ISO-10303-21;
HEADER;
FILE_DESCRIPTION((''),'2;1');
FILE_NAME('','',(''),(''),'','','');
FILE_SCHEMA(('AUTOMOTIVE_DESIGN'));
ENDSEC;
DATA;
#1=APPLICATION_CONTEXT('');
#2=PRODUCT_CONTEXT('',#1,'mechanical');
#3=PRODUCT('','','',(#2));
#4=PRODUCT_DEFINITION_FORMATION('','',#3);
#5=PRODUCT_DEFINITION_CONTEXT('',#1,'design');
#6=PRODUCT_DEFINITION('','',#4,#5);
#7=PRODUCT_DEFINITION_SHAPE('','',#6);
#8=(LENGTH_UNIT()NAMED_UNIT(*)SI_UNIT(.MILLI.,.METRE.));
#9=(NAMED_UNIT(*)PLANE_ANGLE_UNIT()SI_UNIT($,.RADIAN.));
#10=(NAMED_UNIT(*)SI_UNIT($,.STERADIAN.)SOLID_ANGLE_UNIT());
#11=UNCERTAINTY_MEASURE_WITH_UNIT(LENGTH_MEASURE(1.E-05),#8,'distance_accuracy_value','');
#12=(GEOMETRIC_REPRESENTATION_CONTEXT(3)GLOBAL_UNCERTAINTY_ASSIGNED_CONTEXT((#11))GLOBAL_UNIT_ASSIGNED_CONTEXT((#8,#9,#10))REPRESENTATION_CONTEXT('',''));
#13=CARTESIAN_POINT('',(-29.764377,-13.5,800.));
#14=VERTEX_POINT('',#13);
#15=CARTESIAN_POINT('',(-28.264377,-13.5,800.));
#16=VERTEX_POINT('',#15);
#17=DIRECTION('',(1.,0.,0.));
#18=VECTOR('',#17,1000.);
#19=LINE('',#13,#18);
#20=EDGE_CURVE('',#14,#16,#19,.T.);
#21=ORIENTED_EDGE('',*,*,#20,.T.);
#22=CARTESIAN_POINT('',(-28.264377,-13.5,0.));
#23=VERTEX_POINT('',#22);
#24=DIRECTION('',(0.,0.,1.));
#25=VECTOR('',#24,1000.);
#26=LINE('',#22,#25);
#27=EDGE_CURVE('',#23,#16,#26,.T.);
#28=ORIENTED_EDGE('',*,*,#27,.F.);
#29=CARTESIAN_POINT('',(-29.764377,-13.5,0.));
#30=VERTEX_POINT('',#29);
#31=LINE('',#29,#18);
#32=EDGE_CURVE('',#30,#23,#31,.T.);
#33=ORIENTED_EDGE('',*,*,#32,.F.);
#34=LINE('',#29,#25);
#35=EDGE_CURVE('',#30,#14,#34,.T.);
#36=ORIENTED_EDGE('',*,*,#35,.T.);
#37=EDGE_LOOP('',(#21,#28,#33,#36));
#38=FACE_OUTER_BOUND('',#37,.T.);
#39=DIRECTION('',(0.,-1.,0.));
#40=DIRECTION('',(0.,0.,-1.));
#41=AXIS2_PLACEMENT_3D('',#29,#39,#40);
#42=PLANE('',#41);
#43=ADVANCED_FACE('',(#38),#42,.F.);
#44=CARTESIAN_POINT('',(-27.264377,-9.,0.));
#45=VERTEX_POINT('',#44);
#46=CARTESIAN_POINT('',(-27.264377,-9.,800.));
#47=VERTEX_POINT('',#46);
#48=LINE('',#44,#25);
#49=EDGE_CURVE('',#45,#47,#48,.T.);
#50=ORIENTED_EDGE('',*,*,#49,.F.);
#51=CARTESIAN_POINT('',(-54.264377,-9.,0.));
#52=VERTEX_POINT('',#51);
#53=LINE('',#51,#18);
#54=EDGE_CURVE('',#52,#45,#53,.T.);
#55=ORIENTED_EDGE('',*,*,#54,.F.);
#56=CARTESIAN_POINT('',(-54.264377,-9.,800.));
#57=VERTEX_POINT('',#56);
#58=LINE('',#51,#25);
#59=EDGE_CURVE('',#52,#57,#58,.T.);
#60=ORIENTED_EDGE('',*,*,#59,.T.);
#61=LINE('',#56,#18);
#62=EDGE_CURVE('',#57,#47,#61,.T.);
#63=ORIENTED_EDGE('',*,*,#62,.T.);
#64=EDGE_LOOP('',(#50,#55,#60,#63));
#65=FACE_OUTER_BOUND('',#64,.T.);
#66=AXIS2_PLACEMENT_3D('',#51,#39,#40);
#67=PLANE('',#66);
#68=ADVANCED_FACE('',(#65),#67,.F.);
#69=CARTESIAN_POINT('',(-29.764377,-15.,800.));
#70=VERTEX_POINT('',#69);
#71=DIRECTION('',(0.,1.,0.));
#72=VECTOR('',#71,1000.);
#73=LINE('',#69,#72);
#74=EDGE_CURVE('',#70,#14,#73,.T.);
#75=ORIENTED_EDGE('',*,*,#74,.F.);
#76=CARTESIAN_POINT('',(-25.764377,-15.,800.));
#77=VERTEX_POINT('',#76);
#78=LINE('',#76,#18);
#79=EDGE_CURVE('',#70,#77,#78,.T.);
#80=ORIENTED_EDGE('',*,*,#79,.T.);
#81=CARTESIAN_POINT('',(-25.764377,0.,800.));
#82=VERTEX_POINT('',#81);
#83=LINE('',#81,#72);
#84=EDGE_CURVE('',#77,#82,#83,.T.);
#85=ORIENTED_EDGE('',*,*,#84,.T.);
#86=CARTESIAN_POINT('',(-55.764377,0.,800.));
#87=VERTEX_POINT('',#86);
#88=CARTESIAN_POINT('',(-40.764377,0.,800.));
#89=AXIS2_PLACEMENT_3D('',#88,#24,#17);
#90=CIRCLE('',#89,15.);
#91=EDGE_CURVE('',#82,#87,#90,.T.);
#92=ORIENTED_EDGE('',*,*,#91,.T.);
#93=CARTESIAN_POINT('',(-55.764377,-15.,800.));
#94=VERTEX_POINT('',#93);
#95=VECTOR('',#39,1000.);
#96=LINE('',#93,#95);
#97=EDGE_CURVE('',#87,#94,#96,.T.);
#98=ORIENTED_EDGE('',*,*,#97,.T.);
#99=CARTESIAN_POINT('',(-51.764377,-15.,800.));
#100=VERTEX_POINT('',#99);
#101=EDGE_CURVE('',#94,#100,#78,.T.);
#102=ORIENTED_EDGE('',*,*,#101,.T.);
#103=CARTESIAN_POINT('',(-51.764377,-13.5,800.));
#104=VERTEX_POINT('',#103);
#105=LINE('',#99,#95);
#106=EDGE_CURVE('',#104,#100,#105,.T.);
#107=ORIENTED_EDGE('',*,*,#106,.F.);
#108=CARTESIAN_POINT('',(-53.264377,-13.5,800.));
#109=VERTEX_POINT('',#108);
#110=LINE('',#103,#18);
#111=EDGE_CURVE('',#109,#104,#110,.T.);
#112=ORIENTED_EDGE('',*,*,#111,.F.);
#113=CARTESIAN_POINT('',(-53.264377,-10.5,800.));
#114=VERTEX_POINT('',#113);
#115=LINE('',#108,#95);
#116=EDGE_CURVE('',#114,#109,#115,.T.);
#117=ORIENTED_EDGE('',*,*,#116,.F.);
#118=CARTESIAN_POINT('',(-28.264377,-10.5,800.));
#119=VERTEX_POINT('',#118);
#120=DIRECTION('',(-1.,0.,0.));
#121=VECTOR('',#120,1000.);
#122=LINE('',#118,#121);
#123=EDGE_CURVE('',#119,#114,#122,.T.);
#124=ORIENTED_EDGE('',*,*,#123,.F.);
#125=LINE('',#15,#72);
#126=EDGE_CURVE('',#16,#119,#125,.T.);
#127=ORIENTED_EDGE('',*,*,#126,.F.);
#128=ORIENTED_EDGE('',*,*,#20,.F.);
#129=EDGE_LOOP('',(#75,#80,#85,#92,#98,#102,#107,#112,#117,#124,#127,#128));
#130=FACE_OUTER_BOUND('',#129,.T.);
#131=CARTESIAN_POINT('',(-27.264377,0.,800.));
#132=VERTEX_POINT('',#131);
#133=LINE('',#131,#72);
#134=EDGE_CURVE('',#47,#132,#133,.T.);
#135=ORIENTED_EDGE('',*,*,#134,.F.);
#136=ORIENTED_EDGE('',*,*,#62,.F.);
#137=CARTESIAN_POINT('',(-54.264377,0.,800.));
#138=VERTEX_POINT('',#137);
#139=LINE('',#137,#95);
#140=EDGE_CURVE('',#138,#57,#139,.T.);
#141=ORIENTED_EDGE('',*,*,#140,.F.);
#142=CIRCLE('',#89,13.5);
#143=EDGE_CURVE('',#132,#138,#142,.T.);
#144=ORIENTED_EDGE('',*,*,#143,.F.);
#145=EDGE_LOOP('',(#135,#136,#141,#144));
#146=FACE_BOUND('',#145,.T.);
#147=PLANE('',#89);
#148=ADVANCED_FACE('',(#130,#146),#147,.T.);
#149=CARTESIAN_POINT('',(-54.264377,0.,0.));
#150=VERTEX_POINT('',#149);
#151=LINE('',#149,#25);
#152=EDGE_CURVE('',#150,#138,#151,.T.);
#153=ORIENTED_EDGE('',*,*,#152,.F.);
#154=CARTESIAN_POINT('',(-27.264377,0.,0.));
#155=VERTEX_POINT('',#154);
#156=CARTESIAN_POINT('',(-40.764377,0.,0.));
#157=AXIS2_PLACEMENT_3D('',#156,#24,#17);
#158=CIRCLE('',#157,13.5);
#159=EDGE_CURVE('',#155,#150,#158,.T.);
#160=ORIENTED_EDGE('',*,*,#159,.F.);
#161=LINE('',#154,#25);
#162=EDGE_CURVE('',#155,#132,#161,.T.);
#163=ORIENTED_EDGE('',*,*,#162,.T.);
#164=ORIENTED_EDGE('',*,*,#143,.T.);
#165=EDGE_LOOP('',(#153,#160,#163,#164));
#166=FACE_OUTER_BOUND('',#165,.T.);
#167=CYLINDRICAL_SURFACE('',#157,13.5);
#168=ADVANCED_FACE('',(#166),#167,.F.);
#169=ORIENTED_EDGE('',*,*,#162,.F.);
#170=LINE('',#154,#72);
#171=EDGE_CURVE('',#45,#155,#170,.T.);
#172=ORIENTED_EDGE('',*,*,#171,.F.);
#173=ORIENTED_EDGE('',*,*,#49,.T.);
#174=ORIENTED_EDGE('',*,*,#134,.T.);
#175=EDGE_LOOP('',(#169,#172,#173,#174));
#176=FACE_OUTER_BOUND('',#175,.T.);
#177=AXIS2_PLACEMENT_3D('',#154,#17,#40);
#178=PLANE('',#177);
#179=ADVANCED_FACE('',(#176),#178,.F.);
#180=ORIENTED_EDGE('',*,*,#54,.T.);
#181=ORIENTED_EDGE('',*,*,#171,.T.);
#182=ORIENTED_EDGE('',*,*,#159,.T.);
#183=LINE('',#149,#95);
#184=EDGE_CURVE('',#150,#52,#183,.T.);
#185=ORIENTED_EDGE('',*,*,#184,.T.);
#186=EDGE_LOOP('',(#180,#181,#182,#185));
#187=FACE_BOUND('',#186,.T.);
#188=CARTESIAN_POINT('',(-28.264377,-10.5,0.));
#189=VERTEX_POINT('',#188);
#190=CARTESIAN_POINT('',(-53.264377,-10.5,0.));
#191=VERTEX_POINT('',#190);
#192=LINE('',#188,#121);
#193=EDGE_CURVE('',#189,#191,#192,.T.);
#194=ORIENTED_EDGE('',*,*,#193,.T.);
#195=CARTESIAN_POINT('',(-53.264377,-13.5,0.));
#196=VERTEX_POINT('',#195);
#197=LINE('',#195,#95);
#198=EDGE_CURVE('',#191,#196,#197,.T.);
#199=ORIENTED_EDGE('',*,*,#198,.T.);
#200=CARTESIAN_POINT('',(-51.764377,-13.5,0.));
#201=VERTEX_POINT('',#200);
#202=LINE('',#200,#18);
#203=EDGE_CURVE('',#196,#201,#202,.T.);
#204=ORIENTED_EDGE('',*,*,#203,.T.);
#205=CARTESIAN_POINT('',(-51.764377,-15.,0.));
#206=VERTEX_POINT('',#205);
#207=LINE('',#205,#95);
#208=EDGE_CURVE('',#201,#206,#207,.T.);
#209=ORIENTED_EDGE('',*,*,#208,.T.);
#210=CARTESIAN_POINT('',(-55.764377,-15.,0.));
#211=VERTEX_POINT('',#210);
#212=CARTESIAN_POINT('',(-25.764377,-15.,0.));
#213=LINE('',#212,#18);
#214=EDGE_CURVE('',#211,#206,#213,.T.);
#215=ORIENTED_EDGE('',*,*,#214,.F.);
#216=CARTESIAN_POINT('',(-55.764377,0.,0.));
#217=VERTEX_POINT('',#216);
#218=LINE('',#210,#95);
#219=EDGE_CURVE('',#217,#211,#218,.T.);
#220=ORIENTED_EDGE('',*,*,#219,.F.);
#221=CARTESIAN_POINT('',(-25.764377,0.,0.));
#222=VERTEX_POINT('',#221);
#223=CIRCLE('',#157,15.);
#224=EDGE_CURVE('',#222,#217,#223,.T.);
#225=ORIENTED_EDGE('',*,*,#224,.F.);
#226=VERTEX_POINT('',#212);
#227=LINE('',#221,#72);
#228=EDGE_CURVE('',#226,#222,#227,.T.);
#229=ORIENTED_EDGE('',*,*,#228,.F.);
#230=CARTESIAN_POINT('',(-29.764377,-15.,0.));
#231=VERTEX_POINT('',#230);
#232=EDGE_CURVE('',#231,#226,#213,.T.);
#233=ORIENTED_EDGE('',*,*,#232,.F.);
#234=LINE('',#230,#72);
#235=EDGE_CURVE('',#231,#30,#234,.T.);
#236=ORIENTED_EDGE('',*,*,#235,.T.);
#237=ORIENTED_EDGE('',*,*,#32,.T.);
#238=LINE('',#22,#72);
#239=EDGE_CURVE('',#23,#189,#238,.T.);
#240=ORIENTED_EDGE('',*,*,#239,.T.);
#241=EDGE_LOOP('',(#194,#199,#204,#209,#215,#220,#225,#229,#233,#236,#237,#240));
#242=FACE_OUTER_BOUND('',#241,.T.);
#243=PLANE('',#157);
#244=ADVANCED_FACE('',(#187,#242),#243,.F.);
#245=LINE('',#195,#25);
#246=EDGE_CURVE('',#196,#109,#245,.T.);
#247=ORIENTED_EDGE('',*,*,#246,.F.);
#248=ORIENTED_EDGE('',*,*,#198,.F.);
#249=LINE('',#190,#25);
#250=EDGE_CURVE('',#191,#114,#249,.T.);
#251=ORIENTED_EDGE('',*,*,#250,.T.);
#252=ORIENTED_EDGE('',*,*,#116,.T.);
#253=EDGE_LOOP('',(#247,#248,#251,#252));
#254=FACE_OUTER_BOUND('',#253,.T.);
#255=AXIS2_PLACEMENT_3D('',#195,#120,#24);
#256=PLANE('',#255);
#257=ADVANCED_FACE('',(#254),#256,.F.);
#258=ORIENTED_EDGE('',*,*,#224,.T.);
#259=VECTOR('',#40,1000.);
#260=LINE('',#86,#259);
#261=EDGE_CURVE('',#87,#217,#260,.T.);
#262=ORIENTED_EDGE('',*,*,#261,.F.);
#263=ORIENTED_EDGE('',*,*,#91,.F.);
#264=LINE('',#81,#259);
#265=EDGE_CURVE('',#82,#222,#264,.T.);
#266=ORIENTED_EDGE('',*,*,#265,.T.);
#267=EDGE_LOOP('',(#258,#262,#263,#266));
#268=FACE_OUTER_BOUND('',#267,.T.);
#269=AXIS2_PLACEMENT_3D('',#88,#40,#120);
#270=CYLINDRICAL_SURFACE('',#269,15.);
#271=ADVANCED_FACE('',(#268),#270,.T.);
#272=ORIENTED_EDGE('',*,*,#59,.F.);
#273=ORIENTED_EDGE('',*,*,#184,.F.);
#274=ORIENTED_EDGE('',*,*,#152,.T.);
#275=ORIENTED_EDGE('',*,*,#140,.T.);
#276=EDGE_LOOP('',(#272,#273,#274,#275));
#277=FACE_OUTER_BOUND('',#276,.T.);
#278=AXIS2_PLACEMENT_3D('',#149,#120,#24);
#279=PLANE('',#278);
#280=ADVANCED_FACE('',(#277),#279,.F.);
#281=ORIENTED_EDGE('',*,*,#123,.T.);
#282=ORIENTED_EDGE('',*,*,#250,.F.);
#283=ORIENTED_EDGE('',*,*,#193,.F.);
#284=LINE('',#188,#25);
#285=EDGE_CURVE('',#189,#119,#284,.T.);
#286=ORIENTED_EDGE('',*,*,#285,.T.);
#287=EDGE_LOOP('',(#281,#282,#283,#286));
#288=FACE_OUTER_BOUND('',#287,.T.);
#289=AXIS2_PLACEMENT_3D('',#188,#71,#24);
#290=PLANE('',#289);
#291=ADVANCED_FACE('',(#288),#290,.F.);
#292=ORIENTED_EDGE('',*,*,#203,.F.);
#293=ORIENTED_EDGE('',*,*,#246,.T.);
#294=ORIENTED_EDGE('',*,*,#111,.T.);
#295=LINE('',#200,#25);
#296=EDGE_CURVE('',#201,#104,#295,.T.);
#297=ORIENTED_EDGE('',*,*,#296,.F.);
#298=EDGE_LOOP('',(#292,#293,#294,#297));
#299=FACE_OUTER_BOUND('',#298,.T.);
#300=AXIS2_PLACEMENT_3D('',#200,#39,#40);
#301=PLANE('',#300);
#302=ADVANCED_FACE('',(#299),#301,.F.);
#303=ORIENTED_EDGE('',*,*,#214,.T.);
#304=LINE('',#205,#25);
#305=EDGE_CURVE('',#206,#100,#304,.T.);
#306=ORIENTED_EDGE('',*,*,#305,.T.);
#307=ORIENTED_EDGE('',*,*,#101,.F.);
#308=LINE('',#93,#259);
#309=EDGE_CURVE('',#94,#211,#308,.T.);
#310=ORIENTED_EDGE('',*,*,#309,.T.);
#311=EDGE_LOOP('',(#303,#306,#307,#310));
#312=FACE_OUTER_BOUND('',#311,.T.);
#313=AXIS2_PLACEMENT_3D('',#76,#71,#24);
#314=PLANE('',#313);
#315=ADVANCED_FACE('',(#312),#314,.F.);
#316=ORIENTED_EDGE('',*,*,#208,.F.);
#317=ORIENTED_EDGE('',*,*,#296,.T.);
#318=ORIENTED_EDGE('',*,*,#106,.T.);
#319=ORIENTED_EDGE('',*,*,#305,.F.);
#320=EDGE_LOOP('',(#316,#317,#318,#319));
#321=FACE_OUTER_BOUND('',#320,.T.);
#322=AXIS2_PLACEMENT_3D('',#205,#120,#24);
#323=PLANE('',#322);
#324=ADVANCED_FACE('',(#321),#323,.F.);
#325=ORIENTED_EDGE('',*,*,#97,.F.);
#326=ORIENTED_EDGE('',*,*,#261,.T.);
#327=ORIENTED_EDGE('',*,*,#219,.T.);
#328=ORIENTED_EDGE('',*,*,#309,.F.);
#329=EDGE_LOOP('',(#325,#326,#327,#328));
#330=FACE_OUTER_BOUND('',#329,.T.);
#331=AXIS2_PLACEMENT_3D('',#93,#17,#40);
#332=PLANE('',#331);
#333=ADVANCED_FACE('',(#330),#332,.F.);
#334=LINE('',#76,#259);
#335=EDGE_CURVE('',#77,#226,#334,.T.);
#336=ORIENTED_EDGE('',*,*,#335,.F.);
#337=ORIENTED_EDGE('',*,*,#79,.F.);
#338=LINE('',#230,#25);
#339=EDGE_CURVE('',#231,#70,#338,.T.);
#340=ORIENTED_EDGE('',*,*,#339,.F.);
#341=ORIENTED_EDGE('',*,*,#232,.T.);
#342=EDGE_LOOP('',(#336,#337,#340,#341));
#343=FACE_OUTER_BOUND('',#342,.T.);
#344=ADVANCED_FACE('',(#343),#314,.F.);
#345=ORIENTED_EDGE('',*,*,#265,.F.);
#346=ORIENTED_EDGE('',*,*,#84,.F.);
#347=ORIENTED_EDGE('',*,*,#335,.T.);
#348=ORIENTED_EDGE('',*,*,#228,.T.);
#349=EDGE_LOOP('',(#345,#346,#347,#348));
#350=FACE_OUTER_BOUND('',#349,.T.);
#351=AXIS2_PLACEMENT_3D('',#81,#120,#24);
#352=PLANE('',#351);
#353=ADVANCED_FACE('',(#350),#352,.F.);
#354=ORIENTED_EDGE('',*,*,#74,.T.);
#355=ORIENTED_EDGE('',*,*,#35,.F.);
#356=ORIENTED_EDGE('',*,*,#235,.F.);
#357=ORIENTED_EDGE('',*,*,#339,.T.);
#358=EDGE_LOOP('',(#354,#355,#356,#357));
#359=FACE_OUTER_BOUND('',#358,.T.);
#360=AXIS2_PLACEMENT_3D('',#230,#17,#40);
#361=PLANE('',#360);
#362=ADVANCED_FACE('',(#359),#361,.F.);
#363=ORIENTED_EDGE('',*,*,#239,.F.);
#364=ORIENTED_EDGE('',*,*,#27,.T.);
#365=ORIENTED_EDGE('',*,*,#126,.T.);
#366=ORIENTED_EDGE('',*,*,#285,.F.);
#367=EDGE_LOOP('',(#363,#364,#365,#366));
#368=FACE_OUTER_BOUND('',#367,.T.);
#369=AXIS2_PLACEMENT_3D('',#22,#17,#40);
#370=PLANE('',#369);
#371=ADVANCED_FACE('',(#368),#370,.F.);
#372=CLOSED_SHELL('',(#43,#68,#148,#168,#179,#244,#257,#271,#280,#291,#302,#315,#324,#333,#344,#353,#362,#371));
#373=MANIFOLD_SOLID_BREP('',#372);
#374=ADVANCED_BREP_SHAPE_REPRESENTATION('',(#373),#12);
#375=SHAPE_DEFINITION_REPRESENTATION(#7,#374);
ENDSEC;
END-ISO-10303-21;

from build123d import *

# Parameters (mm, degrees)
BOSS_EXTRUDE1_DEPTH = 800
CUT_EXTRUDE1_DEPTH  = 800
CUT_EXTRUDE2_DEPTH  = 803.081458262


with BuildPart() as part:
    # Sketch1 → Boss-Extrude1 (new body)
    with BuildSketch(Plane.XY):
        with BuildLine():
            Line((-25.764376508, 0), (-25.764376508, -15))
            Line((-25.764376508, -15), (-55.764376508, -15))
            Line((-55.764376508, -15), (-55.764376508, 0))
            ThreePointArc((-55.764376508, 0), (-40.764376508, 15), (-25.764376508, 0))
        make_face()
    extrude(amount=BOSS_EXTRUDE1_DEPTH)

    # Sketch2 → Cut-Extrude1 (cut)
    with BuildSketch(Plane.XY.offset(800)):
        with BuildLine():
            Line((-27.264376508, 0), (-27.264376508, -9))
            Line((-27.264376508, -9), (-54.264376508, -9))
            Line((-54.264376508, -9), (-54.264376508, 0))
            ThreePointArc((-54.264376508, 0), (-40.764376508, 13.5), (-27.264376508, 0))
        make_face()
    extrude(amount=-CUT_EXTRUDE1_DEPTH, mode=Mode.SUBTRACT)

    # Sketch3 → Cut-Extrude2 (cut, through all)
    with BuildSketch(Plane.XY.offset(800)):
        Polygon((-51.764376508, -15), (-51.764376508, -13.5), (-53.264376508, -13.5), (-53.264376508, -10.5), (-28.264376508, -10.5), (-28.264376508, -13.5), (-29.764376508, -13.5), (-29.764376508, -15), align=None)
    extrude(amount=-CUT_EXTRUDE2_DEPTH, mode=Mode.SUBTRACT)


solid = part.part
